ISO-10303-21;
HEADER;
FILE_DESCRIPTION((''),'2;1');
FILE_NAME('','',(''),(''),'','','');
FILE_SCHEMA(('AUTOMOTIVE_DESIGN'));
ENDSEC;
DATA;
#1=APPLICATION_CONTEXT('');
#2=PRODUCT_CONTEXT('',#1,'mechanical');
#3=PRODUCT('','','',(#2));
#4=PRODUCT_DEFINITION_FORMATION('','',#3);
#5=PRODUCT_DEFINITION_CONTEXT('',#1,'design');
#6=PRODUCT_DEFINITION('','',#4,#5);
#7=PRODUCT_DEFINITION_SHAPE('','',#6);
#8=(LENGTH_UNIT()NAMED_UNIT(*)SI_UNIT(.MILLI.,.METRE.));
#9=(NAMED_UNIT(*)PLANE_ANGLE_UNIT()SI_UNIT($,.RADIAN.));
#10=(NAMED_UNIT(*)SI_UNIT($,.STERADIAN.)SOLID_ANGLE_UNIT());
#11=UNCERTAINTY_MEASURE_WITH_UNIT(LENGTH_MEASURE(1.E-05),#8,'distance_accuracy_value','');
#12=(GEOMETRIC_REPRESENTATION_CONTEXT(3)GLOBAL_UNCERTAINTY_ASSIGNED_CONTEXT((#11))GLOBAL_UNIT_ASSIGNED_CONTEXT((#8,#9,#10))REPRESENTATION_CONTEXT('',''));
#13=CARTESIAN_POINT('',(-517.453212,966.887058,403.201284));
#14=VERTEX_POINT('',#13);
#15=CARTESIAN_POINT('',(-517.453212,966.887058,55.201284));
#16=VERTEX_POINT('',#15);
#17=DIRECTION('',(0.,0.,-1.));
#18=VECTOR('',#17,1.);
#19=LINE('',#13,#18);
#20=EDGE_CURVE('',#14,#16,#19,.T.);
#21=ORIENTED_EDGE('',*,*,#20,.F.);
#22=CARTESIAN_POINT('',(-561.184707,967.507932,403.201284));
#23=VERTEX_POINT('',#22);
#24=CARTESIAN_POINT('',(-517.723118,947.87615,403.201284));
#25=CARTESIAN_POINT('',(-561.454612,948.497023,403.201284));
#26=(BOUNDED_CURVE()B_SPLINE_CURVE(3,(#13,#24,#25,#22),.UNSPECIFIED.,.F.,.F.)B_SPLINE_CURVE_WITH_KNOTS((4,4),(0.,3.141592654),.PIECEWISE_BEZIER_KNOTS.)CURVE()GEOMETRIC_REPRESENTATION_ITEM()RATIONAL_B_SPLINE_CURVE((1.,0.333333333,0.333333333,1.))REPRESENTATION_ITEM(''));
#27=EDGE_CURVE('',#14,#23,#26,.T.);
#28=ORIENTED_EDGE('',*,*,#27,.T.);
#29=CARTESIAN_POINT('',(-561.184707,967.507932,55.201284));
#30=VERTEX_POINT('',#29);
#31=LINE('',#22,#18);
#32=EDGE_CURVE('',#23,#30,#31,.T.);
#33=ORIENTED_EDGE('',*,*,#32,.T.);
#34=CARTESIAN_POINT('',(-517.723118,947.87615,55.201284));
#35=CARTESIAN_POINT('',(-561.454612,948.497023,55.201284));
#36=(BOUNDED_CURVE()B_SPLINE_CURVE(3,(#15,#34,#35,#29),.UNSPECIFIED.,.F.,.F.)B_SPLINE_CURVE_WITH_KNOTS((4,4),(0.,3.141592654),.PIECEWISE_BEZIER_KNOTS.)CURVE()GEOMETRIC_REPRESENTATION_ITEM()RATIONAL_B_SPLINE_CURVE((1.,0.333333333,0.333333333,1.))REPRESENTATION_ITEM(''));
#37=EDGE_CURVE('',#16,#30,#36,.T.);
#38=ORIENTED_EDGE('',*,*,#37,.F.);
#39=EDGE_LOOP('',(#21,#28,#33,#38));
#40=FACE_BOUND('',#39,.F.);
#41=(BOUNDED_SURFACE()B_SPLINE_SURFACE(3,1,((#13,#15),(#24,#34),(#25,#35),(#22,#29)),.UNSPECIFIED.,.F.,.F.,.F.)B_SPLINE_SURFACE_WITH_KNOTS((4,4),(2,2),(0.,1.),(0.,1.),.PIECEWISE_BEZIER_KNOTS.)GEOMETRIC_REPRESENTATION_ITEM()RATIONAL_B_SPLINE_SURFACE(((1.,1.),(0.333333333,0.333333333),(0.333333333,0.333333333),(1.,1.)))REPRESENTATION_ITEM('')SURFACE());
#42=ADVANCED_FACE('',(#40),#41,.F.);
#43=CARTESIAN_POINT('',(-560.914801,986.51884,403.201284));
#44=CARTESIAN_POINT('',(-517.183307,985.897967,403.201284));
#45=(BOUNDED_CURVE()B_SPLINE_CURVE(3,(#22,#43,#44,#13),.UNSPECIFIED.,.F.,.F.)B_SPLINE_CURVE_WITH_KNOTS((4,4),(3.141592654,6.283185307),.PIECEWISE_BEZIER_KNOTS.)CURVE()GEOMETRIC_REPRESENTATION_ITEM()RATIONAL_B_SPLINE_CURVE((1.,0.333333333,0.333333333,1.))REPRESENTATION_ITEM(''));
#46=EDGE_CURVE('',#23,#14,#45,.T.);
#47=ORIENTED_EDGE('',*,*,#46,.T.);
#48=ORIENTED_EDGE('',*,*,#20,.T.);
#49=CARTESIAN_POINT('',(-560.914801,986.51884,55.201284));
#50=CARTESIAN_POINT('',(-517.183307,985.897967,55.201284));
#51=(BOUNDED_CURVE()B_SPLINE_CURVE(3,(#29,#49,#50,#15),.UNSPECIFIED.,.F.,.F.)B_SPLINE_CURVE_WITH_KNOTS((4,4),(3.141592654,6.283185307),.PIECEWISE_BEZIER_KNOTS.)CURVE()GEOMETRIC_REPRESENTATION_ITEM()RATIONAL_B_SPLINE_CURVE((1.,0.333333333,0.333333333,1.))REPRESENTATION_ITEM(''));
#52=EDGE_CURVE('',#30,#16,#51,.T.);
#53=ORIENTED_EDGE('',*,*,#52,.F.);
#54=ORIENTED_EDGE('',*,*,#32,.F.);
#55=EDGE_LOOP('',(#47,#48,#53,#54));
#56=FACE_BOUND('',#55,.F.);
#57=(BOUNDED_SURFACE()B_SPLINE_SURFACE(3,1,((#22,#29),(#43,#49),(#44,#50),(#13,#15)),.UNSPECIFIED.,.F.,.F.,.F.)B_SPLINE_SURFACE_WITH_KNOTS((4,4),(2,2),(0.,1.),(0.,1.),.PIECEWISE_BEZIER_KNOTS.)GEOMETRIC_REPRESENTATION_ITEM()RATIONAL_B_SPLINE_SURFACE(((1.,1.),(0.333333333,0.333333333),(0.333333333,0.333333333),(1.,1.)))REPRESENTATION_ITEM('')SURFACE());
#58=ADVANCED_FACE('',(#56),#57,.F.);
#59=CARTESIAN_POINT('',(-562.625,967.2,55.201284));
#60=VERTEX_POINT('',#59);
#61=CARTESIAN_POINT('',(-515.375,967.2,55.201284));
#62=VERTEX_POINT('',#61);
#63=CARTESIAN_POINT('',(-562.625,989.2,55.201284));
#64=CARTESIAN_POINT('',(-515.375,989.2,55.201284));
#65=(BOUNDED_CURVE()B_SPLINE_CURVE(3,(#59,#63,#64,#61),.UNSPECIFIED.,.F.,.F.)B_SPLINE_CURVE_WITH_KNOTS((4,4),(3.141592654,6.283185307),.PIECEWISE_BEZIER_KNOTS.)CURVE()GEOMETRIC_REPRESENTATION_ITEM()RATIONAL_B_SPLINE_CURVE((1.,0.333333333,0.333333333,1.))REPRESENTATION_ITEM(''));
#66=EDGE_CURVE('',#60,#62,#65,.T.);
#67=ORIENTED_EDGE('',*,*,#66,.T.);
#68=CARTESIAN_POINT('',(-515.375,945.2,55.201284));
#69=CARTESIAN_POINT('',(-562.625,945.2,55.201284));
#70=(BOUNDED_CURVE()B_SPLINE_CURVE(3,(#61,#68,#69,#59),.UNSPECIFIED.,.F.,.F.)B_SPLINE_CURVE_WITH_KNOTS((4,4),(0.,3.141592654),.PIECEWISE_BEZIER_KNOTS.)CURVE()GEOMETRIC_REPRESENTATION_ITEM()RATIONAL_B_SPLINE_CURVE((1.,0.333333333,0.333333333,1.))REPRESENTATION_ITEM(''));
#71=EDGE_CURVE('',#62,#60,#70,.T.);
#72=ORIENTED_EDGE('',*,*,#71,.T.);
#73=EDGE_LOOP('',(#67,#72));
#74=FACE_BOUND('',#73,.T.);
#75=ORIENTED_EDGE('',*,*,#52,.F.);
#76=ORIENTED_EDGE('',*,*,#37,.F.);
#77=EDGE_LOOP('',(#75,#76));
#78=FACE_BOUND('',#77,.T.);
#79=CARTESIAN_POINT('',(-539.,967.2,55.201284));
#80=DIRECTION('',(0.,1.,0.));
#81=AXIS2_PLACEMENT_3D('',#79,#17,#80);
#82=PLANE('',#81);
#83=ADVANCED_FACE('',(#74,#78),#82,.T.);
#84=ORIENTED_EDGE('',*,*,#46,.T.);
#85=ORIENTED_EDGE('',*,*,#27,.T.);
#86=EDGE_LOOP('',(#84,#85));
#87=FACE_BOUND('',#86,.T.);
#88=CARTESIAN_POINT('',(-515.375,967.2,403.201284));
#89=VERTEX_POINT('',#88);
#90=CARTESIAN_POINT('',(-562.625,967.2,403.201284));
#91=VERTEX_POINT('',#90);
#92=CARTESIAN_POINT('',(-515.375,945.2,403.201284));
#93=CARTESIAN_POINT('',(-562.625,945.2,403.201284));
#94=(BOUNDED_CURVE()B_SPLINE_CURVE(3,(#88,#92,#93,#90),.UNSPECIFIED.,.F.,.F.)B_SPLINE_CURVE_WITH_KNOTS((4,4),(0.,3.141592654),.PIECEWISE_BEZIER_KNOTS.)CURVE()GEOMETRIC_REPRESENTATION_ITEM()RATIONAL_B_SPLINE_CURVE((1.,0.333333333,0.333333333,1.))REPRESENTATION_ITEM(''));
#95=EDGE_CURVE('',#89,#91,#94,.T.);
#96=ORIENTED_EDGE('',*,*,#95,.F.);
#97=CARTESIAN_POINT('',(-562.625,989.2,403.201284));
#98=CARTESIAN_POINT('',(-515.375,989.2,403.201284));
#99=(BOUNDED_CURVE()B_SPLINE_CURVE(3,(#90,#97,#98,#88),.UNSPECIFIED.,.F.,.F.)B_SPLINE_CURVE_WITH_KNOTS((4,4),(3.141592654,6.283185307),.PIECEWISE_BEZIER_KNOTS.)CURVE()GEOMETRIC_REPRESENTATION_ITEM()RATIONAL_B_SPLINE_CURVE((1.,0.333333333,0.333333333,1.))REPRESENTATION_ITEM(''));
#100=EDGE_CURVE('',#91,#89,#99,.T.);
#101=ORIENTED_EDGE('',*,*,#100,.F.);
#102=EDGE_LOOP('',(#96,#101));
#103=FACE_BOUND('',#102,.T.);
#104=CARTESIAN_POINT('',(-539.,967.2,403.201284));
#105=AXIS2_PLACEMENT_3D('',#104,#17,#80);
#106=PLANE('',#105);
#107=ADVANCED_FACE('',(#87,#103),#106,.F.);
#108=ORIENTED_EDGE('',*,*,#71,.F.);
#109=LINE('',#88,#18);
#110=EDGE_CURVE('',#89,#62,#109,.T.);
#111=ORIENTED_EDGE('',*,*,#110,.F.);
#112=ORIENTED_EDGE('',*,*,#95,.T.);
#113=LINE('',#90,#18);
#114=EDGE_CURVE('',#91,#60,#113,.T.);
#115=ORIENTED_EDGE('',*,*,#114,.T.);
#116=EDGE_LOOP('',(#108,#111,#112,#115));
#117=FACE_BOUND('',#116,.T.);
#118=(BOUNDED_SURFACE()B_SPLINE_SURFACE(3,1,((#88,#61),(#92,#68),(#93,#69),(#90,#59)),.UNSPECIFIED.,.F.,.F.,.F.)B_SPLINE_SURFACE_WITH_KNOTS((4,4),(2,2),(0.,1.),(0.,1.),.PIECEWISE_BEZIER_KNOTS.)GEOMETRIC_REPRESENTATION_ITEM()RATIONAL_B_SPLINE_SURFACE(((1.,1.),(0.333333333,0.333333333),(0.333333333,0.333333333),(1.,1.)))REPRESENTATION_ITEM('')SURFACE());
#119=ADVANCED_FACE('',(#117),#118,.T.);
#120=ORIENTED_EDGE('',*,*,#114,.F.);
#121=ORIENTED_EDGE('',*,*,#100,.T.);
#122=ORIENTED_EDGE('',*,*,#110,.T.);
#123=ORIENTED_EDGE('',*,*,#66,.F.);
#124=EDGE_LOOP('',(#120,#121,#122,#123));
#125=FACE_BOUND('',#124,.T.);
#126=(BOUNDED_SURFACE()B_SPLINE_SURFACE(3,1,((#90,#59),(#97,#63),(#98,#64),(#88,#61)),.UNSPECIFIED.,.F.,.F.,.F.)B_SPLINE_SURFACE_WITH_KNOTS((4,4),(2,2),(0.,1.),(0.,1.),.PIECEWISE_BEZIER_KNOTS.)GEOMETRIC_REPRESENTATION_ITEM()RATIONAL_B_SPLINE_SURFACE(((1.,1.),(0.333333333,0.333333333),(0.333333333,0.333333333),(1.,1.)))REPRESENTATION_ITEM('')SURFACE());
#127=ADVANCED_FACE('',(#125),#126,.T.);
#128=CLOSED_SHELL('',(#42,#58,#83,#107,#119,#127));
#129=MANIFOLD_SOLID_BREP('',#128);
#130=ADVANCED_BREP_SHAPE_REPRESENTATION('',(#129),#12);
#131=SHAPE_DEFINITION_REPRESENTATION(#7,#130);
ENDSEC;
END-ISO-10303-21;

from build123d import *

# Parameters (mm, degrees)
SKETCH1_RX          = 23.625
SKETCH1_RY          = 11
SKETCH1_RX_2        = 21.86795069
SKETCH1_RY_2        = 9.506412044
BOSS_EXTRUDE1_DEPTH = 348


with BuildPart() as part:
    # Sketch1 → Boss-Extrude1 (new body)
    with BuildSketch(Plane(origin=(0, 0, 55.201283758), x_dir=(-1, 0, 0), z_dir=(0, 0, -1))):
        with Locations(Location((539, 967.2), (0, 0, 180))):
            Ellipse(SKETCH1_RX, SKETCH1_RY)
        with Locations(Location((539.318959601, 967.197494981), (0, 0, -179.186603951))):
            Ellipse(SKETCH1_RX_2, SKETCH1_RY_2, mode=Mode.SUBTRACT)
    extrude(amount=-BOSS_EXTRUDE1_DEPTH)


solid = part.part
